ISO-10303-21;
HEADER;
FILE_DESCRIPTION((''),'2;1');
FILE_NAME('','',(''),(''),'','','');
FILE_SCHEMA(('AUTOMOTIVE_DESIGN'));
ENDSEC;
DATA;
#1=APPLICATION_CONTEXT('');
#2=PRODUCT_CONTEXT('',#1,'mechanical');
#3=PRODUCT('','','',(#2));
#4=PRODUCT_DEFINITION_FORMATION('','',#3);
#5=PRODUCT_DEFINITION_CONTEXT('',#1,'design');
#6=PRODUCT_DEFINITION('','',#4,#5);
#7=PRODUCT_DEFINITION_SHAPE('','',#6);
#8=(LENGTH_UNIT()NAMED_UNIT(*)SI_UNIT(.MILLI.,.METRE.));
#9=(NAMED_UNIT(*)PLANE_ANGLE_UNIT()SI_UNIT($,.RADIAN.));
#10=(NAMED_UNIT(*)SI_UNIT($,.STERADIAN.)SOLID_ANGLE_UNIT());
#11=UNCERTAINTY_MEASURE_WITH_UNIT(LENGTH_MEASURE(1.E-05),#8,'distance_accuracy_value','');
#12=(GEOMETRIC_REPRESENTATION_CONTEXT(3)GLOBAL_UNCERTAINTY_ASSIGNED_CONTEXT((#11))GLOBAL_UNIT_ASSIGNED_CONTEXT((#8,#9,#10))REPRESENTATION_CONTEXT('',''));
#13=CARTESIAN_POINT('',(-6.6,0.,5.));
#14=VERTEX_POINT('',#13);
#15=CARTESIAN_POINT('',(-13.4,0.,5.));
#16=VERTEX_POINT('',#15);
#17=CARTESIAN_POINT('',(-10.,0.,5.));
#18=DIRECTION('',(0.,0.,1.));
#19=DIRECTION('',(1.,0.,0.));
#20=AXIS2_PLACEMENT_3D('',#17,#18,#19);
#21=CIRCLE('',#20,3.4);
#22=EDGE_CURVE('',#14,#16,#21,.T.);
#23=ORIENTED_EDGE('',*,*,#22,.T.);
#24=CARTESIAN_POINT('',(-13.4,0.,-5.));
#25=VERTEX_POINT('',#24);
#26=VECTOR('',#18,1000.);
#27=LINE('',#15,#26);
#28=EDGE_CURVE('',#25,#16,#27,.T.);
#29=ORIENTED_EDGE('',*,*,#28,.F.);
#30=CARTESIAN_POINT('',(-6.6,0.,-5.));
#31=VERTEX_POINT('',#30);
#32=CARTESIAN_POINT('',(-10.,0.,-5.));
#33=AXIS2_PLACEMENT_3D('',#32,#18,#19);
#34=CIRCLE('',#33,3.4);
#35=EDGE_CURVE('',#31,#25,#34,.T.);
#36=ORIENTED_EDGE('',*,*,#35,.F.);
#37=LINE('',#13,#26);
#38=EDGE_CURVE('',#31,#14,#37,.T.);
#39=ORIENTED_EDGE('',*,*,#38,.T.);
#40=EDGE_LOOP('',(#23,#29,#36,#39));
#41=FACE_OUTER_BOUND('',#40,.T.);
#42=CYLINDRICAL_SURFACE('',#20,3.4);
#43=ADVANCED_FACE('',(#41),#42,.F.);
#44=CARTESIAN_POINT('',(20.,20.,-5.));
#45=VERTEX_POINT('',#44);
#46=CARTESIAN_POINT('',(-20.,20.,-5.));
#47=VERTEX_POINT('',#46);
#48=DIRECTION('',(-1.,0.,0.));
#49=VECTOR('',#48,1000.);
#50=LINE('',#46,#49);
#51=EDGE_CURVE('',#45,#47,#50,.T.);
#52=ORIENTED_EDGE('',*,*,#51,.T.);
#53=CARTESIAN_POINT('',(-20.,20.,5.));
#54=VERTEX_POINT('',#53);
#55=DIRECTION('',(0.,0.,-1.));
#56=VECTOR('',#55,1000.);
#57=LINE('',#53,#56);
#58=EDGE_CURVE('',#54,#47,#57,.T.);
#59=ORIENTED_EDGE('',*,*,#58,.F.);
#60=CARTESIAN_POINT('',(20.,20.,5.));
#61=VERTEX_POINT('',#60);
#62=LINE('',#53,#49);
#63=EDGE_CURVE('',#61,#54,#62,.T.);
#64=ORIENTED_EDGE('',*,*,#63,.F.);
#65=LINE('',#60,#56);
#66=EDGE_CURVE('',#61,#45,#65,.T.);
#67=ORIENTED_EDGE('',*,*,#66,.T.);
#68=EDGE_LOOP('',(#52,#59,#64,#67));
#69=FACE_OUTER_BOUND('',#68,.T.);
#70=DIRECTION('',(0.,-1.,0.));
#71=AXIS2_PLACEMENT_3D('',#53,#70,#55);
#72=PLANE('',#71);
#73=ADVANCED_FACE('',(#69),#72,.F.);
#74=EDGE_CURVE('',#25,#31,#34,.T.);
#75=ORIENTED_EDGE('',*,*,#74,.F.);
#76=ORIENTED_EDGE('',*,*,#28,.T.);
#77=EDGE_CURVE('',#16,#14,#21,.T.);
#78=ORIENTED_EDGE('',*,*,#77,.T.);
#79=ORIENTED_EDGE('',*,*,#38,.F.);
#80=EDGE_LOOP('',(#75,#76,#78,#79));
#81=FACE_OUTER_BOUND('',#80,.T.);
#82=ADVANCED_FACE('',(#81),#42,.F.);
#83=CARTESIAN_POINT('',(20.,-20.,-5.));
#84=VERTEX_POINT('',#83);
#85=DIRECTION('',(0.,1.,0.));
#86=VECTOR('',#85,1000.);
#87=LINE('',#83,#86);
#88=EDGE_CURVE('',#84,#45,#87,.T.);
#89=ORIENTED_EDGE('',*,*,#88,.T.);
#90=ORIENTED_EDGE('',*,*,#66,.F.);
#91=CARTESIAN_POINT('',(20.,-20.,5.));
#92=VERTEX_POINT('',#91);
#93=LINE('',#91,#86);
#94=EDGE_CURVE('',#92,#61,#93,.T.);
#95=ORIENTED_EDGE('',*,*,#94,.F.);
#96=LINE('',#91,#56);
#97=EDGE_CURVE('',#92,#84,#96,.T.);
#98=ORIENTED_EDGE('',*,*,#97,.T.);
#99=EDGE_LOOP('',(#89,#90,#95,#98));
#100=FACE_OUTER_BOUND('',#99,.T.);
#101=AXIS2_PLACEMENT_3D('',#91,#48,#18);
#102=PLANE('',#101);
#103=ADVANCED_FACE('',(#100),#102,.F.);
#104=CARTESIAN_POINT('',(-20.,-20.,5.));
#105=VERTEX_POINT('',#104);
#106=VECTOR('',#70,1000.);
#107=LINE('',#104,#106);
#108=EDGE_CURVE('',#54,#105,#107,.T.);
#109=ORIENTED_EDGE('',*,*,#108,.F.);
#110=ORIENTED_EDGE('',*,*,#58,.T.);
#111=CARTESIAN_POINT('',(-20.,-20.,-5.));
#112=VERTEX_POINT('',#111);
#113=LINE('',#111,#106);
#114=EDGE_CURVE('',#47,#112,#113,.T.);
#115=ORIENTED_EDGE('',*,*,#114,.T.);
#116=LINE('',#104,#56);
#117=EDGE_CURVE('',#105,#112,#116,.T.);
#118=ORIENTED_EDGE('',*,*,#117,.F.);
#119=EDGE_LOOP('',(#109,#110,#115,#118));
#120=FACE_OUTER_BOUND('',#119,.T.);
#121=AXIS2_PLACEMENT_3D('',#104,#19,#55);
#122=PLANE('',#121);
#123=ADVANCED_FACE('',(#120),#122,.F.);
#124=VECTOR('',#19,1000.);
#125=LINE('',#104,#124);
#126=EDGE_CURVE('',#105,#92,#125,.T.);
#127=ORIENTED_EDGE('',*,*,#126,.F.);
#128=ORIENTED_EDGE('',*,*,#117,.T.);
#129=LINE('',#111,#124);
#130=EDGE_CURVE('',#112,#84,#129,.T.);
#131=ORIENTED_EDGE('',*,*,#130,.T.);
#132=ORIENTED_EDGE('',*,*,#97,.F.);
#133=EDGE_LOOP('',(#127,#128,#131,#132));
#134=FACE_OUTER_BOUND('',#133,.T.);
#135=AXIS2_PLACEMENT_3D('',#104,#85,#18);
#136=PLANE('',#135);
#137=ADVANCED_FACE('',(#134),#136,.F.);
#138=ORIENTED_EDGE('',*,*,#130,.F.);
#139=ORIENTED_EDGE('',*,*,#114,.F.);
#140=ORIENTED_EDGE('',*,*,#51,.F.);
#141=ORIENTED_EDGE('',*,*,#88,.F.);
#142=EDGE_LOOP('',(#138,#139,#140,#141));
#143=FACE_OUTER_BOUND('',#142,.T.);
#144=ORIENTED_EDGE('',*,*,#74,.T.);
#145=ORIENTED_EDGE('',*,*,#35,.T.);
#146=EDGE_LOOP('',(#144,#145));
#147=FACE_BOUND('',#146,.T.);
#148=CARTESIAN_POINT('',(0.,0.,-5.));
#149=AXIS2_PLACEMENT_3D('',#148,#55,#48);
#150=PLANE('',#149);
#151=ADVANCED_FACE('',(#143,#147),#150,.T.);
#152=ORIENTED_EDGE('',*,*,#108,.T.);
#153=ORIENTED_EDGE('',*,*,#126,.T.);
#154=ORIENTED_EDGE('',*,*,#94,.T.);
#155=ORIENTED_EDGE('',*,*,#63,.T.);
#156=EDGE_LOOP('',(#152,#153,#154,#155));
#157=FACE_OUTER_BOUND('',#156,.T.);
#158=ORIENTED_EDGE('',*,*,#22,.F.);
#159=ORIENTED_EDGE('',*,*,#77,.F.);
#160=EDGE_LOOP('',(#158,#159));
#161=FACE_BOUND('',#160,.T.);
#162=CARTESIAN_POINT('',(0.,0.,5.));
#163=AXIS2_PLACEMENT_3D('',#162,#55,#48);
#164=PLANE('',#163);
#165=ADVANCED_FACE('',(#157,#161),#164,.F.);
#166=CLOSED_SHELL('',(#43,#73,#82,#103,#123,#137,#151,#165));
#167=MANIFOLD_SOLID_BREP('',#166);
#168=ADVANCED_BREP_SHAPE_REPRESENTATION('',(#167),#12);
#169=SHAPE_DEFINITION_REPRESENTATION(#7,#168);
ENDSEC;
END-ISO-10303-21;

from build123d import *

# Parameters (mm, degrees)
SKETCH_1_W         = 40
SKETCH_1_H         = 40
EXTRUDE_1_DEPTH    = 5
HOLE_WIZARD_M8_1_D = 6.8


with BuildPart() as part:
    # 草图1 → 凸台-拉伸1 (new, symmetric)
    with BuildSketch(Plane.XY):
        Rectangle(SKETCH_1_W, SKETCH_1_H)
    extrude(amount=EXTRUDE_1_DEPTH, both=True)

    # M8 螺纹孔1 (through all)
    with Locations(Plane.XY.offset(5)):
        with Locations((-10, 0)):
            Hole(HOLE_WIZARD_M8_1_D / 2)


solid = part.part
